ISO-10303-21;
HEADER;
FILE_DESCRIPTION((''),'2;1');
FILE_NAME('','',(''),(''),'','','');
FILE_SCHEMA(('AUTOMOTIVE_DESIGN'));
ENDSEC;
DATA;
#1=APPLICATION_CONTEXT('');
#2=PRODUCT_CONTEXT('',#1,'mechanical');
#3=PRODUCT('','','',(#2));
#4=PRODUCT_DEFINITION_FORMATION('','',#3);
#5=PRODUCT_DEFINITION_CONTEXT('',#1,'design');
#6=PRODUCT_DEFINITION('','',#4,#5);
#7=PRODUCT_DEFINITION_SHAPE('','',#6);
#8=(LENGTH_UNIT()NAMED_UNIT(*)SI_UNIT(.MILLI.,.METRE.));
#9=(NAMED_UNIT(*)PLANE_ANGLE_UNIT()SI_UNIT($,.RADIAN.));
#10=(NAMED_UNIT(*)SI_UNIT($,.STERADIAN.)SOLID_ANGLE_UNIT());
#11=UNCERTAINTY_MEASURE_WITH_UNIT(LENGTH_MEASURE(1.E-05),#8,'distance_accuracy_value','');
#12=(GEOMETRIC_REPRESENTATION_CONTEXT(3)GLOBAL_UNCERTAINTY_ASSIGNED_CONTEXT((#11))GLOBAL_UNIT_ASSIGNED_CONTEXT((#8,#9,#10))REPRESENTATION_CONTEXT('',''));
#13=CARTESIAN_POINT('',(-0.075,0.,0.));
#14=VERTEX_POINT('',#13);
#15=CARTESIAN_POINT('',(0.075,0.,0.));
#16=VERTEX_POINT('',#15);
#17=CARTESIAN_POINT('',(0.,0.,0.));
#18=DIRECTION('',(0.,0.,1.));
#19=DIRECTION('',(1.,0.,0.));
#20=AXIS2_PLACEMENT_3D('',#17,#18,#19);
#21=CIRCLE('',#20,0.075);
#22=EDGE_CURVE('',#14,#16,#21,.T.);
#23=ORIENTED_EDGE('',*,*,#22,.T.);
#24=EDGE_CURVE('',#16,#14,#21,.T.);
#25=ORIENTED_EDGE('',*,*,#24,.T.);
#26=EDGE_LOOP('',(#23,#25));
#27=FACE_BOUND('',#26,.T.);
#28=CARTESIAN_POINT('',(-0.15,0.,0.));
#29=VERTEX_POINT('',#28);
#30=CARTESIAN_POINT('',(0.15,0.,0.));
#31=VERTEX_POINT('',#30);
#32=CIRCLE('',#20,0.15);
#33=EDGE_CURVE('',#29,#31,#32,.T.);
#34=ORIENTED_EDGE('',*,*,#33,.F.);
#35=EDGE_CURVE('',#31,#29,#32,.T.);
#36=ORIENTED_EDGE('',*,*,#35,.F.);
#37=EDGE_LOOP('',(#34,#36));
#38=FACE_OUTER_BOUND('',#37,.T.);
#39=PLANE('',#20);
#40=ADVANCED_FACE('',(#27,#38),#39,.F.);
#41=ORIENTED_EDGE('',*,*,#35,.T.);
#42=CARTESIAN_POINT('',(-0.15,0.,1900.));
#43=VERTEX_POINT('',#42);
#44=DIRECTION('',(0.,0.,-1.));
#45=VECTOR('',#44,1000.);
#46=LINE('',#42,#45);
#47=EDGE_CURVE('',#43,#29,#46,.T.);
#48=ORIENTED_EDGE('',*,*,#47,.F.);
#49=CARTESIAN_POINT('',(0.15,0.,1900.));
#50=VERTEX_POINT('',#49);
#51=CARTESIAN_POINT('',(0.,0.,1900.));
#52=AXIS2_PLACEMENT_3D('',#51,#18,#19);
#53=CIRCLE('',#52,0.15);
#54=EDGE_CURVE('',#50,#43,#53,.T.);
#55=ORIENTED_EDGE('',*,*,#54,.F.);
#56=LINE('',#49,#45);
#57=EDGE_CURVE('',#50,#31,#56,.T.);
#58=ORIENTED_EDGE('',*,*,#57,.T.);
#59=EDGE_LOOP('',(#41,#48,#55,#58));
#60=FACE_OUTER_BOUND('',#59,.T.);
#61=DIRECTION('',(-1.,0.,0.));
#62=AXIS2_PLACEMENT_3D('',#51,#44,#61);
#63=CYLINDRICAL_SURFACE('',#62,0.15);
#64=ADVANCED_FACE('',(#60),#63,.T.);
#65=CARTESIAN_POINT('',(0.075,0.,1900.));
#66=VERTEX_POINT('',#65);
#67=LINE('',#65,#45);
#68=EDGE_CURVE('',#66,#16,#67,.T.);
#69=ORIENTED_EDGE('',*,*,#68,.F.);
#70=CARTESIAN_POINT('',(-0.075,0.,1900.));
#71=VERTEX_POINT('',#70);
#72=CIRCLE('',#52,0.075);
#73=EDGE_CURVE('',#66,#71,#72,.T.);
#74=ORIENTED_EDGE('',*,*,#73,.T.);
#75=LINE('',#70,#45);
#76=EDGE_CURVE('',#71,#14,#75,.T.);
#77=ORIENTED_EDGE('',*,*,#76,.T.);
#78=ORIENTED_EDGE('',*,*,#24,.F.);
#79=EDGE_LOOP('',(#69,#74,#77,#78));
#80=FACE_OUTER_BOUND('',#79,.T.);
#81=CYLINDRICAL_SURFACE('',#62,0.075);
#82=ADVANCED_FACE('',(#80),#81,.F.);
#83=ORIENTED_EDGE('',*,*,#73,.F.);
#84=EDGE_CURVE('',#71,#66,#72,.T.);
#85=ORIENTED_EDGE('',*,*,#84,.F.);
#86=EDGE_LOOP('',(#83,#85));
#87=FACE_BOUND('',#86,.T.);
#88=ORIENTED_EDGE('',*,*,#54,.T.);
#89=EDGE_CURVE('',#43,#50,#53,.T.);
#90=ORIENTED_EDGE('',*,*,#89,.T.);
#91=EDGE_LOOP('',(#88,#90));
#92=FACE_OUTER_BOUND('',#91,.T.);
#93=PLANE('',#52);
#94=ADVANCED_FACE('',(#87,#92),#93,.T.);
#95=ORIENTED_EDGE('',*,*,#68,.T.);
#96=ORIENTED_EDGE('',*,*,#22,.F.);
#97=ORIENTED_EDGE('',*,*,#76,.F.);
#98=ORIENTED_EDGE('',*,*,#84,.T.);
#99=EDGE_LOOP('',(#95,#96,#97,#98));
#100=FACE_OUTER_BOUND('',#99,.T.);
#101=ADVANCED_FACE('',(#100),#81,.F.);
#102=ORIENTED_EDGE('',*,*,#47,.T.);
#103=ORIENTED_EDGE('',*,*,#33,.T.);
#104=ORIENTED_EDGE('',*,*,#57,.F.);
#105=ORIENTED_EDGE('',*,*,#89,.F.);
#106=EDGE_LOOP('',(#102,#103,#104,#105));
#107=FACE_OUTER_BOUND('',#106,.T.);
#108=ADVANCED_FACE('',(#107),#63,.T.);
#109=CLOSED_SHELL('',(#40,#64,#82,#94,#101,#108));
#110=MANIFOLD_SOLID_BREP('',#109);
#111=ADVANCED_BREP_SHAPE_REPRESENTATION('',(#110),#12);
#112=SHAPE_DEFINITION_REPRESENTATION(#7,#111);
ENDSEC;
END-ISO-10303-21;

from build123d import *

# Parameters (mm, degrees)
SKETCH1_R           = 0.15
SKETCH1_R_2         = 0.075
BOSS_EXTRUDE1_DEPTH = 1900


with BuildPart() as part:
    # Sketch1 → Boss-Extrude1 (new body)
    with BuildSketch(Plane.XY):
        Circle(SKETCH1_R)
        Circle(SKETCH1_R_2, mode=Mode.SUBTRACT)
    extrude(amount=BOSS_EXTRUDE1_DEPTH)


solid = part.part
